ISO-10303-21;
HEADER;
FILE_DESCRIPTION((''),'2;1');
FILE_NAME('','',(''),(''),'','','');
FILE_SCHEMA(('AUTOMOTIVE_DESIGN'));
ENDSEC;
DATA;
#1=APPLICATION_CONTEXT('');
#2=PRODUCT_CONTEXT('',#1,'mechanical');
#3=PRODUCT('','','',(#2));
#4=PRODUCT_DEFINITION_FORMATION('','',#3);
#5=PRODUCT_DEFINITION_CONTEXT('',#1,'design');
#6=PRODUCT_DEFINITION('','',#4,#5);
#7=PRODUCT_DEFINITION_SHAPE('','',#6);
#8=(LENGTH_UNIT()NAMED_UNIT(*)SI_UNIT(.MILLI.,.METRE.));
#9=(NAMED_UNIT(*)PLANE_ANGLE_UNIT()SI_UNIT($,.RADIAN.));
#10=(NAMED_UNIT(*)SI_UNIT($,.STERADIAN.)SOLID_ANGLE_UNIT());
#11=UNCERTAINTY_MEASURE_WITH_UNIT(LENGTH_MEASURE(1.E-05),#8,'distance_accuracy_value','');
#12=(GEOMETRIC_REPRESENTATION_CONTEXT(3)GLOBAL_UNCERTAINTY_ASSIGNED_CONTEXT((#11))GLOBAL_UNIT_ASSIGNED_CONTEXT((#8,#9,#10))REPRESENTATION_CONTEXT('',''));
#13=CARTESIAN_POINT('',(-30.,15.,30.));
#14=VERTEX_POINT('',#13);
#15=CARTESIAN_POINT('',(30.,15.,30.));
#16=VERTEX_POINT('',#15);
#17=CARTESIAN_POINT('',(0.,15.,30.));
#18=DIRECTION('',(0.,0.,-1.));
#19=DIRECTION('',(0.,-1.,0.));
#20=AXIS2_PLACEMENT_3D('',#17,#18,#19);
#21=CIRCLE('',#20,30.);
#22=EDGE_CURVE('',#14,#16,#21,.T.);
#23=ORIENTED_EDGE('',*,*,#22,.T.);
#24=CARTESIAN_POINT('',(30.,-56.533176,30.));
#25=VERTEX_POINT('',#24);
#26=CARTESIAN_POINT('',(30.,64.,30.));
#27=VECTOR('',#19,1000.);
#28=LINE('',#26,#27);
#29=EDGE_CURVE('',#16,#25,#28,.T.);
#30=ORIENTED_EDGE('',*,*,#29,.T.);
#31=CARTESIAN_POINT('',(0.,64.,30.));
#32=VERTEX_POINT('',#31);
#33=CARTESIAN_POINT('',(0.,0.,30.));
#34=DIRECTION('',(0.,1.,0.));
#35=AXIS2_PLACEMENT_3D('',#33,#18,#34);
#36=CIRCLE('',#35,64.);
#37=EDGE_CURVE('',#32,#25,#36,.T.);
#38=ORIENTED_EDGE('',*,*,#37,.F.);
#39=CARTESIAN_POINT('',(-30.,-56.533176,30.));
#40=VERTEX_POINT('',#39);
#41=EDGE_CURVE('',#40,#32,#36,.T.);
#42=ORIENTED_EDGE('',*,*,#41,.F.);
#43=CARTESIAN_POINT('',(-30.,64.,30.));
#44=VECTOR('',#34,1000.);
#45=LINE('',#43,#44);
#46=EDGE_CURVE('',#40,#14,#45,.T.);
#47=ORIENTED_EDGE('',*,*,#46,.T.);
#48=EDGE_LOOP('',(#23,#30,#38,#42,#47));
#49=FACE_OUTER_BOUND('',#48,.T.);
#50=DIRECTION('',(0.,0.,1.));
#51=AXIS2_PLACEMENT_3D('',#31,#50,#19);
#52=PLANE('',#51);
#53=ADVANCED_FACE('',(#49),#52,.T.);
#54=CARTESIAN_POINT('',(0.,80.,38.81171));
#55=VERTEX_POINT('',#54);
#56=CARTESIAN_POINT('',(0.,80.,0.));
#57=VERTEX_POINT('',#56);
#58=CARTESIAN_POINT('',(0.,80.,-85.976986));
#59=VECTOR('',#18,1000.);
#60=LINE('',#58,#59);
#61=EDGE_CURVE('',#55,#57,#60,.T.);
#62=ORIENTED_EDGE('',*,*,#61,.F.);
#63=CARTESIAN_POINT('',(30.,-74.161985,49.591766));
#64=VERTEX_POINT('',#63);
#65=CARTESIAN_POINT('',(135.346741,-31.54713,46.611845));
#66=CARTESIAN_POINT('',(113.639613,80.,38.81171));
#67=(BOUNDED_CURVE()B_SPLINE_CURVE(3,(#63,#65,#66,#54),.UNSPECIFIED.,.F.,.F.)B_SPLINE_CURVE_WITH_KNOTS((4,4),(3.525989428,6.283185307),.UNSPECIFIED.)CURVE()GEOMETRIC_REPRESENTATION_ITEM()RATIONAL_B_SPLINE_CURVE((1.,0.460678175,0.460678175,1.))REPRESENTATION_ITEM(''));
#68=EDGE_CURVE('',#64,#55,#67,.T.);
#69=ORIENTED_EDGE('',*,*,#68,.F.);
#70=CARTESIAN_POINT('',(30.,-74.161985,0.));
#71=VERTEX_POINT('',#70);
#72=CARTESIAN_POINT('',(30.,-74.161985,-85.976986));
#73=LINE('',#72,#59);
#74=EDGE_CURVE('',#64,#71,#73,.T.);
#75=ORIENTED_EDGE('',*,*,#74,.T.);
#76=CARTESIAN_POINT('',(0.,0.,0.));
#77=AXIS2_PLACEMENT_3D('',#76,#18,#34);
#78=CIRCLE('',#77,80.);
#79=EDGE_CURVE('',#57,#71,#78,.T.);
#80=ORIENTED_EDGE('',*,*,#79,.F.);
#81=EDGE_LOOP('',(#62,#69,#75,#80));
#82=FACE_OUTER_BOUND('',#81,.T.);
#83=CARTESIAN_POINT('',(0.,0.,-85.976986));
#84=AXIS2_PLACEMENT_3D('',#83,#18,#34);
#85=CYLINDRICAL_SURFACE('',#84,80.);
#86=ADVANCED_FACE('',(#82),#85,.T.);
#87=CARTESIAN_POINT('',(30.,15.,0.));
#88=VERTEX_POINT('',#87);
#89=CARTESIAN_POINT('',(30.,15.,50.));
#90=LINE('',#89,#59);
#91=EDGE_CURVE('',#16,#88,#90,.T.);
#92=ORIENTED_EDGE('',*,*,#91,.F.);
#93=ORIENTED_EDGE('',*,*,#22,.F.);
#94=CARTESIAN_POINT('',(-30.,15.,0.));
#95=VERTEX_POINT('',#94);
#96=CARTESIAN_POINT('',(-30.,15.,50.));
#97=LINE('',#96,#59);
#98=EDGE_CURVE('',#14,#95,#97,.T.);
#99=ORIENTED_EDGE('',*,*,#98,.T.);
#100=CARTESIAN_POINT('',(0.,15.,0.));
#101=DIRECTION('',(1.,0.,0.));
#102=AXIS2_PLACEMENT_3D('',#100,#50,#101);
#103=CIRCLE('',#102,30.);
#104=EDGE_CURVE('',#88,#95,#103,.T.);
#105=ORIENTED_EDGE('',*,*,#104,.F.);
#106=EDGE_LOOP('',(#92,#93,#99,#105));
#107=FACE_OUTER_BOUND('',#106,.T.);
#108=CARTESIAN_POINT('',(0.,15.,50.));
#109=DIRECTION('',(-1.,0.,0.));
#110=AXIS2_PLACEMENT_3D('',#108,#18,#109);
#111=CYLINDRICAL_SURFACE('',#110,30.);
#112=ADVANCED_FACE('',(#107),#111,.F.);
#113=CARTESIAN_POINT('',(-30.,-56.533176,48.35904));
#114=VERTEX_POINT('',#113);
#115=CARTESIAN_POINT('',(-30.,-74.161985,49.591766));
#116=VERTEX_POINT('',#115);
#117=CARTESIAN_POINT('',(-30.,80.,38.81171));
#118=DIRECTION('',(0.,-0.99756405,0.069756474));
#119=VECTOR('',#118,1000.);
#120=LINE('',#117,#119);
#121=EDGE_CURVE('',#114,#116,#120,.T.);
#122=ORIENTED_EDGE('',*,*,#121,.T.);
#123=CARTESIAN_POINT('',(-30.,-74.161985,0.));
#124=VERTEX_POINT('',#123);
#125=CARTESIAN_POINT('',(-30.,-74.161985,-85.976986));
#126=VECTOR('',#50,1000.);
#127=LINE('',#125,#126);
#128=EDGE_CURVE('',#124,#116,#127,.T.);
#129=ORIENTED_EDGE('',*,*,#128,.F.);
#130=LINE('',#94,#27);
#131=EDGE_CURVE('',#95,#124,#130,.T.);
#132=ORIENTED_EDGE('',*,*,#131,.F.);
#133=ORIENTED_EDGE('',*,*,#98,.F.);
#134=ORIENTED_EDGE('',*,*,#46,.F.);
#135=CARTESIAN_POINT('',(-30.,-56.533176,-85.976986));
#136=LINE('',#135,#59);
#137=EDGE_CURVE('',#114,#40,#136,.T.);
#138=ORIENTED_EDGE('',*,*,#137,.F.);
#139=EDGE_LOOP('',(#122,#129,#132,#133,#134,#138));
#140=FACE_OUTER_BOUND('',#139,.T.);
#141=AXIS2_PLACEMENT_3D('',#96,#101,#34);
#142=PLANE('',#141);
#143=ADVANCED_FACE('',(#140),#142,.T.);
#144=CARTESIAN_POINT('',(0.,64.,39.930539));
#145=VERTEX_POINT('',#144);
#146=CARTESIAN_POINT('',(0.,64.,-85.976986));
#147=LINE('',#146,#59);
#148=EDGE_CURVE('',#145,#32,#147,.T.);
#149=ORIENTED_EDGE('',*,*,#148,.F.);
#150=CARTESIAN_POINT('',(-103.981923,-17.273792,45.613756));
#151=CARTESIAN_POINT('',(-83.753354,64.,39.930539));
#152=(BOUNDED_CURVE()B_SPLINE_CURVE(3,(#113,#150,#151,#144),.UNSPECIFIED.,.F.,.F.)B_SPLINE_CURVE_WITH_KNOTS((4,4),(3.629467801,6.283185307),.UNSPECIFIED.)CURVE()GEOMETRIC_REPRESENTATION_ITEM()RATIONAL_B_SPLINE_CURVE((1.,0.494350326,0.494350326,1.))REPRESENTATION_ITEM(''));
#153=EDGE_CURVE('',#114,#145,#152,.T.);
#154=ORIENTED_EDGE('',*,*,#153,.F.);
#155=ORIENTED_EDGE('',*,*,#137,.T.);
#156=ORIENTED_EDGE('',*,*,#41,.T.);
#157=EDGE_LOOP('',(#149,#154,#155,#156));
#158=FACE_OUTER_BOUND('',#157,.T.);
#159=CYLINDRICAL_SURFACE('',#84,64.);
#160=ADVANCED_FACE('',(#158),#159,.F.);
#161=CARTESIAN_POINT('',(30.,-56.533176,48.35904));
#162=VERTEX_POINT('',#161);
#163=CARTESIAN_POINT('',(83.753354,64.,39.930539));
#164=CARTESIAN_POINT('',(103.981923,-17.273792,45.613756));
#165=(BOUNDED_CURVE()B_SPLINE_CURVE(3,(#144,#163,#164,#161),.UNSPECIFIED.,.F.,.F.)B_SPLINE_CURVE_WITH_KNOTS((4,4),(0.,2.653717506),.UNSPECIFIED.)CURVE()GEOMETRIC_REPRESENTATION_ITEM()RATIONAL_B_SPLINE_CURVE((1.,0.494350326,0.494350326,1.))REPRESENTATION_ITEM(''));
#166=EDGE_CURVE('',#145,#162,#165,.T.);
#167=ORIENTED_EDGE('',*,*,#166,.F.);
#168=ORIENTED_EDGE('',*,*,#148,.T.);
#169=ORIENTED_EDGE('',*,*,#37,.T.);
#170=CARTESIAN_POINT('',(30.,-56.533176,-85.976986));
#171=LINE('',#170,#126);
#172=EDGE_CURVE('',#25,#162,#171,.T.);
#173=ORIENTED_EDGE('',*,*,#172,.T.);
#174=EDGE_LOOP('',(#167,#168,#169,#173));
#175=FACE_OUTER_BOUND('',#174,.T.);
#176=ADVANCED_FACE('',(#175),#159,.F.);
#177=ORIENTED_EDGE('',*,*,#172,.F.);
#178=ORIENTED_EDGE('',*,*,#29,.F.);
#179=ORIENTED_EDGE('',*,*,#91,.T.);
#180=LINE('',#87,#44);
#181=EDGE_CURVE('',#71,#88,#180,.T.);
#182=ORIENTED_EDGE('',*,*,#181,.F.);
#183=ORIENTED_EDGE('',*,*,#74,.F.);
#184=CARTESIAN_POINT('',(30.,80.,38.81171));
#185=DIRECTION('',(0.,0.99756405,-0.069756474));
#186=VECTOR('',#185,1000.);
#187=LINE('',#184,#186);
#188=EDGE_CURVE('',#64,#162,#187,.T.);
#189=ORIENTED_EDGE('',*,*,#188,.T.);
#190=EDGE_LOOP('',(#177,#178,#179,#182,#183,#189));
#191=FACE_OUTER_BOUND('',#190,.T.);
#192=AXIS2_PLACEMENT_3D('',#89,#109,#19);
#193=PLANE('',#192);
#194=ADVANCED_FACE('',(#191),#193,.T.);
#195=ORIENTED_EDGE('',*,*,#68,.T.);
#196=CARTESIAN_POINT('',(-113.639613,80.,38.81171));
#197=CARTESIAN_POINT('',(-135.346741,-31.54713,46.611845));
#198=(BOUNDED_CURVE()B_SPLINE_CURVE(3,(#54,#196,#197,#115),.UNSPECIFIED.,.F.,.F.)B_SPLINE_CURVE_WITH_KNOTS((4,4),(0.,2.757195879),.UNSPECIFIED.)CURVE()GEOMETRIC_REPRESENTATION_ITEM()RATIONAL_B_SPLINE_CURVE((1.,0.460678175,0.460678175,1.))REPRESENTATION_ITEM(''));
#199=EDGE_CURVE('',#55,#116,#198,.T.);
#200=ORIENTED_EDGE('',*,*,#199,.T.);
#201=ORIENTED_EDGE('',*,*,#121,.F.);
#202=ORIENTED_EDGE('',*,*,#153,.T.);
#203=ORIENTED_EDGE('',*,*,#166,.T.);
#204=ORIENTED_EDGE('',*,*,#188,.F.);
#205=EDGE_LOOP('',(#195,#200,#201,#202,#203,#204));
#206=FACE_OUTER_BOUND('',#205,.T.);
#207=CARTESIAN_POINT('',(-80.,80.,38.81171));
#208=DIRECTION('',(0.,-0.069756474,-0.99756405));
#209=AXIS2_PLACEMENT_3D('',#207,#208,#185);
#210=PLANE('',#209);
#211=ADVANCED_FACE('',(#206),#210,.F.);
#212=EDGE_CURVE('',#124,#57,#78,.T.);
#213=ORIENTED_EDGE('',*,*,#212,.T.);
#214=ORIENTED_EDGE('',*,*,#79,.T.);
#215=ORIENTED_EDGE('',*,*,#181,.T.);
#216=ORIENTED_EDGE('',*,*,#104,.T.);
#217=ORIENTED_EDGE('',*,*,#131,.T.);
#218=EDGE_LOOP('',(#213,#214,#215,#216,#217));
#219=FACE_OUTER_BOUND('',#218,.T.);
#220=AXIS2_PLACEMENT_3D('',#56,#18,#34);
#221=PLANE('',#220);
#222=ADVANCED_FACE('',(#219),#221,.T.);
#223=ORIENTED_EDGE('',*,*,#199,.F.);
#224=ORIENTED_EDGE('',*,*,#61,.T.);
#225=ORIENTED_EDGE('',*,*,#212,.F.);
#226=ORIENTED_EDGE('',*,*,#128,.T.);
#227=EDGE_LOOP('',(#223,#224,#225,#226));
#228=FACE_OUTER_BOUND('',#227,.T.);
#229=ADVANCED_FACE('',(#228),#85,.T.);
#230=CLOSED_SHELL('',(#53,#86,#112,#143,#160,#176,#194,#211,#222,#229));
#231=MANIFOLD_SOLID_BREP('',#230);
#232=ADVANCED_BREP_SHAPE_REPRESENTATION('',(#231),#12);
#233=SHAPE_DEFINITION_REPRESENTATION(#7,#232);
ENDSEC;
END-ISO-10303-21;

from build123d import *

# Parameters (mm, degrees)
CUT_EXTRUDE1_DEPTH      = 124.693168769
CUT_EXTRUDE1_DEPTH_BACK = 124.693168769
CUT_EXTRUDE2_DEPTH      = 124.693168769


with BuildPart() as part:
    # Sketch1 → Revolve2 (revolve)
    with BuildSketch(Plane(origin=(0, 0, 0), x_dir=(0, 0, -1), z_dir=(1, 0, 0))):
        Polygon((-50, 64), (-50, 80), (0, 80), (0, 0), (-30, 0), (-30, 64), align=None)
    revolve(axis=Axis((0, 0, -85.976986238), (0, 0, 1)))

    # Sketch2 → Cut-Extrude1 (cut, two sides: drawn at the far end of the back side and taken through both)
    with BuildSketch(Plane(origin=(0, 0, 0), x_dir=(0, 0, -1), z_dir=(1, 0, 0)).offset(-CUT_EXTRUDE1_DEPTH_BACK)):
        Polygon((-50, 80), (-38.811710089, 80), (-50, -80), align=None)
    extrude(amount=CUT_EXTRUDE1_DEPTH + CUT_EXTRUDE1_DEPTH_BACK, mode=Mode.SUBTRACT)

    # Sketch3 → Cut-Extrude2 (cut, through all)
    with BuildSketch(Plane.XY):
        with BuildLine():
            Line((30, 15), (30, -100))
            ThreePointArc((30, -100), (0, -130), (-30, -100))
            Line((-30, -100), (-30, 15))
            ThreePointArc((-30, 15), (0, 45), (30, 15))
        make_face()
    extrude(amount=CUT_EXTRUDE2_DEPTH, mode=Mode.SUBTRACT)


solid = part.part
